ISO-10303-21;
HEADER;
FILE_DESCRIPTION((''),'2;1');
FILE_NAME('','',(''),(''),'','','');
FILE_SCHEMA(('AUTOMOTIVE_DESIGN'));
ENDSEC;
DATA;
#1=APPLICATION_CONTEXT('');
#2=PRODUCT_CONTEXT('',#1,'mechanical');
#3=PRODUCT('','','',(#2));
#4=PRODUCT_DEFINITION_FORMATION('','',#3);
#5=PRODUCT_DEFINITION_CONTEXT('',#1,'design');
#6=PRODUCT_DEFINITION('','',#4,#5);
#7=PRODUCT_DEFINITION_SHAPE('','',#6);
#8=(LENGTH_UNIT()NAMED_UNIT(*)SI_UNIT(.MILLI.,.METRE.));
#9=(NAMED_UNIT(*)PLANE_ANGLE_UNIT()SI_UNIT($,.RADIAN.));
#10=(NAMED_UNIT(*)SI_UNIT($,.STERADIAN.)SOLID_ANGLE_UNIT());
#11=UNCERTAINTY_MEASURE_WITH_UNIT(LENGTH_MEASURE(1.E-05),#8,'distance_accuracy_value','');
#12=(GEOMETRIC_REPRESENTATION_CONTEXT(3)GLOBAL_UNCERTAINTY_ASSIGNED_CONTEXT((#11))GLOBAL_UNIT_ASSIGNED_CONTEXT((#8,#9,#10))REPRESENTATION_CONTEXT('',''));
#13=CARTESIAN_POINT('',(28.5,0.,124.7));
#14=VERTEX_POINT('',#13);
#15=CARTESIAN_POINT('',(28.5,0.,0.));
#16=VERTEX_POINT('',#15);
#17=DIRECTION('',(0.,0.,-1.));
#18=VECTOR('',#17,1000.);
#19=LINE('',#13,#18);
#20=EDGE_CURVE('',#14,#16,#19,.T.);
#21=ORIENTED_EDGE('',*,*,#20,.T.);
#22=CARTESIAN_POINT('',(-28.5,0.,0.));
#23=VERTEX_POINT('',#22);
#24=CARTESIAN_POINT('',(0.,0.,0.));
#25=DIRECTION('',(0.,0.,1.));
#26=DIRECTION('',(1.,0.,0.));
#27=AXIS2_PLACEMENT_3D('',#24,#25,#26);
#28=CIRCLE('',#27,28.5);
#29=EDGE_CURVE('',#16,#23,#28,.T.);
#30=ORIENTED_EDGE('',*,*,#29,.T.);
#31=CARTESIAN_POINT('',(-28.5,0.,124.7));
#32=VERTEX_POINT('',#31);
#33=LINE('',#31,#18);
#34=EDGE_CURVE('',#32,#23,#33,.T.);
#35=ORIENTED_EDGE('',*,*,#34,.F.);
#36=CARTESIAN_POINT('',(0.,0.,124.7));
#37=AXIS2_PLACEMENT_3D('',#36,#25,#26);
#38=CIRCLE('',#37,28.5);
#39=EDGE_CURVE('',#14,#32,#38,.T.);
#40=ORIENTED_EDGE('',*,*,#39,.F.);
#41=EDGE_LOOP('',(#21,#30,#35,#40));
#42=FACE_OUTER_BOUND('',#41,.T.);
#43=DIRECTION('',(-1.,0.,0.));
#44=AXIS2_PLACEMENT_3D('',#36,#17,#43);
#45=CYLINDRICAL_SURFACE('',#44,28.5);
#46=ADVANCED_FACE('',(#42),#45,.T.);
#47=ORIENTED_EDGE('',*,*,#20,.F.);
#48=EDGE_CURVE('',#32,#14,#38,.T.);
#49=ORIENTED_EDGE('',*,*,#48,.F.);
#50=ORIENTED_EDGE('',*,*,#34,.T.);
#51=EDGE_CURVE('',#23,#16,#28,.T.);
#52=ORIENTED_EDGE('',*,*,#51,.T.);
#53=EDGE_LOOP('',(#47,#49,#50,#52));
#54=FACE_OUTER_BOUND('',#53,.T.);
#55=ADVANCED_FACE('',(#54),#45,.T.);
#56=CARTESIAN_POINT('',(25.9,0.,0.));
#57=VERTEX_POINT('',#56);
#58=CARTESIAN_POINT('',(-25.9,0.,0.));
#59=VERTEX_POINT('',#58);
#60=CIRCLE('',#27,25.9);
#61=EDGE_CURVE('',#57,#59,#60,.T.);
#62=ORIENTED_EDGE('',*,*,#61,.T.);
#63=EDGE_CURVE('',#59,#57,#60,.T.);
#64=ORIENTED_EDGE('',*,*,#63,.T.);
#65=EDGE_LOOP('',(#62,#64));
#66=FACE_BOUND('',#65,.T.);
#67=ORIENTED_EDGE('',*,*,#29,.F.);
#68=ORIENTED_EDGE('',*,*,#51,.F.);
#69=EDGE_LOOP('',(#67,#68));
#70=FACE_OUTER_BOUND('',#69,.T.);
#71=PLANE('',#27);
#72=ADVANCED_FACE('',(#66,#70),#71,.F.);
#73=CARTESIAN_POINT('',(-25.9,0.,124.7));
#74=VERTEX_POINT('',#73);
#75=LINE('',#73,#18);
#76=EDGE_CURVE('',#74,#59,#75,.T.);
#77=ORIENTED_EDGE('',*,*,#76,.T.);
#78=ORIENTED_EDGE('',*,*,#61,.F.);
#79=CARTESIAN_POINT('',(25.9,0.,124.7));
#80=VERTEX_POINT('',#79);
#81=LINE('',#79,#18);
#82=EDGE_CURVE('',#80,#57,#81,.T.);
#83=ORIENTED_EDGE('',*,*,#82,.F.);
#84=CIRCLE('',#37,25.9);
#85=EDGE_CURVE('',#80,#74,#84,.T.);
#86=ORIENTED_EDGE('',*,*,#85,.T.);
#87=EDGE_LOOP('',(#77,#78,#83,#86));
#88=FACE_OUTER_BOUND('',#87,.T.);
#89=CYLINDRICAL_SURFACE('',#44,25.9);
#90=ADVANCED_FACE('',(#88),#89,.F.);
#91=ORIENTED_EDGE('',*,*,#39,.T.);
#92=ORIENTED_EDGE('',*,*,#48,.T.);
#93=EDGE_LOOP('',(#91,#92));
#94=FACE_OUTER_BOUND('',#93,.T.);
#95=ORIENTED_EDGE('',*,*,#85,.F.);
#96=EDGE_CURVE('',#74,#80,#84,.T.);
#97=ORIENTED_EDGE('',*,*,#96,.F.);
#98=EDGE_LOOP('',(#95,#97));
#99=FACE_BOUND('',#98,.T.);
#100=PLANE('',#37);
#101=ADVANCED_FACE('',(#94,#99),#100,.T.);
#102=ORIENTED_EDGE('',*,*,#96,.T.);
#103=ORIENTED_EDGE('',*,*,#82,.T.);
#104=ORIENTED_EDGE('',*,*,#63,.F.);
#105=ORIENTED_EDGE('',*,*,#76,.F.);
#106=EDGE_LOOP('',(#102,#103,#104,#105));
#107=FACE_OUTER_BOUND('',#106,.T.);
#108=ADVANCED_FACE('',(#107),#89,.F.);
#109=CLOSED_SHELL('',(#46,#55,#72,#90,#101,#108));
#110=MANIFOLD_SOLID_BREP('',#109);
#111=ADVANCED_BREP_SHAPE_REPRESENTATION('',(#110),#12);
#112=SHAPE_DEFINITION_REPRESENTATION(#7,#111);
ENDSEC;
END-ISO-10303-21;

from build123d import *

# Parameters (mm, degrees)
SKETCH1_R           = 28.5
SKETCH1_R_2         = 25.9
EXTRUDE_THIN1_DEPTH = 124.7


with BuildPart() as part:
    # Sketch1 → Extrude-Thin1 (new body)
    with BuildSketch(Plane.XY):
        Circle(SKETCH1_R)
        Circle(SKETCH1_R_2, mode=Mode.SUBTRACT)
    extrude(amount=EXTRUDE_THIN1_DEPTH)


solid = part.part
